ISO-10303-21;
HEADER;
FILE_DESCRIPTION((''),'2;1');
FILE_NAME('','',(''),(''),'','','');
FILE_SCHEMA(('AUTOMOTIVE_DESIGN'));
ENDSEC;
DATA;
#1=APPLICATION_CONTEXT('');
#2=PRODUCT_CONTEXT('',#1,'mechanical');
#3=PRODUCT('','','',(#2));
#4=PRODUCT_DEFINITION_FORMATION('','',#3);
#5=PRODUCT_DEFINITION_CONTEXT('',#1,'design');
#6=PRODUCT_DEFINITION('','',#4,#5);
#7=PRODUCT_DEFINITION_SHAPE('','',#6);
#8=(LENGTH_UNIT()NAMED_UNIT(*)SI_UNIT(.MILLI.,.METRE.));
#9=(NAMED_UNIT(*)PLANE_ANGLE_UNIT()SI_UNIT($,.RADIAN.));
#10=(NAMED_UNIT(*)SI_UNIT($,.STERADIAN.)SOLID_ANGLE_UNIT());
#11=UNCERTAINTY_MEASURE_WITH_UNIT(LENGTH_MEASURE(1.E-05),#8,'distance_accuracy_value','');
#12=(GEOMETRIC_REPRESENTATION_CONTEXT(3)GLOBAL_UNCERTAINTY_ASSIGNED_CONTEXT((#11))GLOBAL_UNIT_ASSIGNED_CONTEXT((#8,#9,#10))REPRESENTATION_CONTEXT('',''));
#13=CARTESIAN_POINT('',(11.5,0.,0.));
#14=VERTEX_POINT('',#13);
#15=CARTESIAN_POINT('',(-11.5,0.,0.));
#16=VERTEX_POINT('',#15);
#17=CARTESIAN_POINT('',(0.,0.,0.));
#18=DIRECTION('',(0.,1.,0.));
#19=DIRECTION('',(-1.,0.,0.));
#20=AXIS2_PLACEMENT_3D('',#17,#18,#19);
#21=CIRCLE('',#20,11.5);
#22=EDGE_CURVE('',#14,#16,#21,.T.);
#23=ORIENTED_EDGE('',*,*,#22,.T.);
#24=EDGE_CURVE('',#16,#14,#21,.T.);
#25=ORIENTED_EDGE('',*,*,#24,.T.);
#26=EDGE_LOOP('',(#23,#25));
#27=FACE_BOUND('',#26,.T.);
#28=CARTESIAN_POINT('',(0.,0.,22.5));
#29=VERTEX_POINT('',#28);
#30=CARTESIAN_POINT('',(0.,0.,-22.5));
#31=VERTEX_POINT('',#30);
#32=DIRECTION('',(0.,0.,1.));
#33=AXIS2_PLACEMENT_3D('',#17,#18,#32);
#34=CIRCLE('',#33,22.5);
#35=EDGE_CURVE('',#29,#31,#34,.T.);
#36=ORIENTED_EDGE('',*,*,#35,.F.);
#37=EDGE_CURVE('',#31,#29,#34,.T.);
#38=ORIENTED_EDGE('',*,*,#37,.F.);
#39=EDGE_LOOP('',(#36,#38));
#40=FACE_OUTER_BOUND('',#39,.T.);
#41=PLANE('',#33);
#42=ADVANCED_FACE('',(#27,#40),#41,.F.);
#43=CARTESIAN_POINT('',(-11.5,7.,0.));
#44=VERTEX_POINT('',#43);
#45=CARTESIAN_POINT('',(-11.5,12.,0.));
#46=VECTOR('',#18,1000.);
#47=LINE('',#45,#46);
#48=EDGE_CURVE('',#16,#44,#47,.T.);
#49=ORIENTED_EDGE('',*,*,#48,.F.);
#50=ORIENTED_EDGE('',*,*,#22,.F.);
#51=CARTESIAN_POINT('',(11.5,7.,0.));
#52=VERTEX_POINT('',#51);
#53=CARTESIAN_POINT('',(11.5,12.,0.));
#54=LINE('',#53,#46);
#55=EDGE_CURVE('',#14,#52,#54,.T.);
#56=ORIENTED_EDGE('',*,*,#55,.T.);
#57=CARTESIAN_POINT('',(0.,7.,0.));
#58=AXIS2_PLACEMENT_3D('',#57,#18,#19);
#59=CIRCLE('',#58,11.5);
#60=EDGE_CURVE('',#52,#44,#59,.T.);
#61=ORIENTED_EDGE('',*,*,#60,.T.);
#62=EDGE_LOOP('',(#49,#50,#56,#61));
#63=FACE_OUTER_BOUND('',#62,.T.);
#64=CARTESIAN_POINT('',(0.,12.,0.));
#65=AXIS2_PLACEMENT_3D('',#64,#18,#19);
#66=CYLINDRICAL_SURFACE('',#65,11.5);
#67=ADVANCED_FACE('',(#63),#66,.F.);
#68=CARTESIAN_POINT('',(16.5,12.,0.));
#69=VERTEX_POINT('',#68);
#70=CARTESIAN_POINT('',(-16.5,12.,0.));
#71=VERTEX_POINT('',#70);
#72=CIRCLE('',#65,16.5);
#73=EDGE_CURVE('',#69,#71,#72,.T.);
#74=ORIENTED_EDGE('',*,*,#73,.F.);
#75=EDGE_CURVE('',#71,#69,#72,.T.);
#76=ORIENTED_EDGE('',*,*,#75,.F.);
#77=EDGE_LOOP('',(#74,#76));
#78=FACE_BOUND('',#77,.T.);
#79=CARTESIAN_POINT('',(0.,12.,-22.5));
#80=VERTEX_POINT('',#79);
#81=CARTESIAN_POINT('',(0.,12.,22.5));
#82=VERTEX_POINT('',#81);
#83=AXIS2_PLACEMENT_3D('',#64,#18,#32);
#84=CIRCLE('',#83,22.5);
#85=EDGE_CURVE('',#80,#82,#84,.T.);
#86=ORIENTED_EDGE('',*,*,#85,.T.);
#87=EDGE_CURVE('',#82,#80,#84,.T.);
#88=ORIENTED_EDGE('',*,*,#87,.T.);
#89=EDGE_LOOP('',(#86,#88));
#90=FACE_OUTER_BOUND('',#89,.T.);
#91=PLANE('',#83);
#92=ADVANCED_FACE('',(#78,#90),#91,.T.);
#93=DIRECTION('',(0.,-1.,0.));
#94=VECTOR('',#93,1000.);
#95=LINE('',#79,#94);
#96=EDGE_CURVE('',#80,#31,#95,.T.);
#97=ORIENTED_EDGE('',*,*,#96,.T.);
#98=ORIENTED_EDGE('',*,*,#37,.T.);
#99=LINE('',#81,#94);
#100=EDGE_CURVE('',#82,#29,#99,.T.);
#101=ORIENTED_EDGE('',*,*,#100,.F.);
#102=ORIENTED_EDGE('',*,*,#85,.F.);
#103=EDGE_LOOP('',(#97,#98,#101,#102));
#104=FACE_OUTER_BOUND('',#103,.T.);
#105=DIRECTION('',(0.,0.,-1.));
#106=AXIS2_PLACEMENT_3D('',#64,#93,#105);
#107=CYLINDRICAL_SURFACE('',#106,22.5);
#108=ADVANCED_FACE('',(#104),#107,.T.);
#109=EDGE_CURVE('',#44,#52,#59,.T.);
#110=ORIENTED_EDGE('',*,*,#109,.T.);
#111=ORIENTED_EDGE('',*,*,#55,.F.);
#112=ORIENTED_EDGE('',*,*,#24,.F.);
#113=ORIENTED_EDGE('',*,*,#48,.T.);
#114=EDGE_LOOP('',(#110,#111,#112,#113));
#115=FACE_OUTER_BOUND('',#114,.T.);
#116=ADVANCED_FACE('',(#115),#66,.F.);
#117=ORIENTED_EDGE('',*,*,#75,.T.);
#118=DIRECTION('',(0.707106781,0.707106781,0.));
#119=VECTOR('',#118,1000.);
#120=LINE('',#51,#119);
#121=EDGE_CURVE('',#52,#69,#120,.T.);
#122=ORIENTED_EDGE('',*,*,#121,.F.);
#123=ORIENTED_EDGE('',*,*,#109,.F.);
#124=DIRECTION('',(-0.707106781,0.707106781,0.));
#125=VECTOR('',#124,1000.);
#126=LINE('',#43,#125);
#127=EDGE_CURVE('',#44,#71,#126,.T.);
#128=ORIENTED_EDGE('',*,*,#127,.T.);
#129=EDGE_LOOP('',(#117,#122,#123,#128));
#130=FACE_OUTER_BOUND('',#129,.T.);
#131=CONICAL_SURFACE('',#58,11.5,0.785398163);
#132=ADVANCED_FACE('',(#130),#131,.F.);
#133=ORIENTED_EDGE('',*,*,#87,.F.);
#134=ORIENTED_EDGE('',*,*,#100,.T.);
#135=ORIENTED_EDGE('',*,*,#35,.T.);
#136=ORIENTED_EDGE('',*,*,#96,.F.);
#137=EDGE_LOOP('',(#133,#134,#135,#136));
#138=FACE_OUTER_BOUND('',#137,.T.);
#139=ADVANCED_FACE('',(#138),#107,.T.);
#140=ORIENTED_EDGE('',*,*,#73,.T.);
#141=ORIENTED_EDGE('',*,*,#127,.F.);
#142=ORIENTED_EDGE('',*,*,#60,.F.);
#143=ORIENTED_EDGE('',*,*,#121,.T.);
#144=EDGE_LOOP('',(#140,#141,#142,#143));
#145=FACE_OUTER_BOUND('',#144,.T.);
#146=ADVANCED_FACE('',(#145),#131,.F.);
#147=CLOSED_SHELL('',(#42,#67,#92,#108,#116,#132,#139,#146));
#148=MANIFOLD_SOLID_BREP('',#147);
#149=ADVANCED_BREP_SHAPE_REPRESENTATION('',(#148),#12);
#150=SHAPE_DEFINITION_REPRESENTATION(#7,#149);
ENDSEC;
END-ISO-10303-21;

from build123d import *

# Parameters (mm, degrees)
BUSH_OD_PROFILE_45_R  = 22.5
BUSH_BODY_45X12_DEPTH = 12


with BuildPart() as part:
    # Bush OD Profile Ø45 → Bush Body Ø45x12 (new body)
    with BuildSketch(Plane(origin=(0, 0, 0), x_dir=(1, 0, 0), z_dir=(0, 1, 0))):
        with Locations(Location((0, 0, 0), (0, 0, 270))):
            Circle(BUSH_OD_PROFILE_45_R)
    extrude(amount=BUSH_BODY_45X12_DEPTH)

    # Countersunk Bore Profile → Countersunk Bore (revolve, cut)
    with BuildSketch(Plane.XY, mode=Mode.PRIVATE) as countersunk_bore_sk:
        Polygon((11.5, 0), (11.5, 7), (16.5, 12), (0, 12), (0, 0), align=None)
    revolve(countersunk_bore_sk.sketch.rotate(Axis((0, 12, 0), (0, -1, 0)), 180), axis=Axis((0, 12, 0), (0, -1, 0)), mode=Mode.SUBTRACT)


solid = part.part
